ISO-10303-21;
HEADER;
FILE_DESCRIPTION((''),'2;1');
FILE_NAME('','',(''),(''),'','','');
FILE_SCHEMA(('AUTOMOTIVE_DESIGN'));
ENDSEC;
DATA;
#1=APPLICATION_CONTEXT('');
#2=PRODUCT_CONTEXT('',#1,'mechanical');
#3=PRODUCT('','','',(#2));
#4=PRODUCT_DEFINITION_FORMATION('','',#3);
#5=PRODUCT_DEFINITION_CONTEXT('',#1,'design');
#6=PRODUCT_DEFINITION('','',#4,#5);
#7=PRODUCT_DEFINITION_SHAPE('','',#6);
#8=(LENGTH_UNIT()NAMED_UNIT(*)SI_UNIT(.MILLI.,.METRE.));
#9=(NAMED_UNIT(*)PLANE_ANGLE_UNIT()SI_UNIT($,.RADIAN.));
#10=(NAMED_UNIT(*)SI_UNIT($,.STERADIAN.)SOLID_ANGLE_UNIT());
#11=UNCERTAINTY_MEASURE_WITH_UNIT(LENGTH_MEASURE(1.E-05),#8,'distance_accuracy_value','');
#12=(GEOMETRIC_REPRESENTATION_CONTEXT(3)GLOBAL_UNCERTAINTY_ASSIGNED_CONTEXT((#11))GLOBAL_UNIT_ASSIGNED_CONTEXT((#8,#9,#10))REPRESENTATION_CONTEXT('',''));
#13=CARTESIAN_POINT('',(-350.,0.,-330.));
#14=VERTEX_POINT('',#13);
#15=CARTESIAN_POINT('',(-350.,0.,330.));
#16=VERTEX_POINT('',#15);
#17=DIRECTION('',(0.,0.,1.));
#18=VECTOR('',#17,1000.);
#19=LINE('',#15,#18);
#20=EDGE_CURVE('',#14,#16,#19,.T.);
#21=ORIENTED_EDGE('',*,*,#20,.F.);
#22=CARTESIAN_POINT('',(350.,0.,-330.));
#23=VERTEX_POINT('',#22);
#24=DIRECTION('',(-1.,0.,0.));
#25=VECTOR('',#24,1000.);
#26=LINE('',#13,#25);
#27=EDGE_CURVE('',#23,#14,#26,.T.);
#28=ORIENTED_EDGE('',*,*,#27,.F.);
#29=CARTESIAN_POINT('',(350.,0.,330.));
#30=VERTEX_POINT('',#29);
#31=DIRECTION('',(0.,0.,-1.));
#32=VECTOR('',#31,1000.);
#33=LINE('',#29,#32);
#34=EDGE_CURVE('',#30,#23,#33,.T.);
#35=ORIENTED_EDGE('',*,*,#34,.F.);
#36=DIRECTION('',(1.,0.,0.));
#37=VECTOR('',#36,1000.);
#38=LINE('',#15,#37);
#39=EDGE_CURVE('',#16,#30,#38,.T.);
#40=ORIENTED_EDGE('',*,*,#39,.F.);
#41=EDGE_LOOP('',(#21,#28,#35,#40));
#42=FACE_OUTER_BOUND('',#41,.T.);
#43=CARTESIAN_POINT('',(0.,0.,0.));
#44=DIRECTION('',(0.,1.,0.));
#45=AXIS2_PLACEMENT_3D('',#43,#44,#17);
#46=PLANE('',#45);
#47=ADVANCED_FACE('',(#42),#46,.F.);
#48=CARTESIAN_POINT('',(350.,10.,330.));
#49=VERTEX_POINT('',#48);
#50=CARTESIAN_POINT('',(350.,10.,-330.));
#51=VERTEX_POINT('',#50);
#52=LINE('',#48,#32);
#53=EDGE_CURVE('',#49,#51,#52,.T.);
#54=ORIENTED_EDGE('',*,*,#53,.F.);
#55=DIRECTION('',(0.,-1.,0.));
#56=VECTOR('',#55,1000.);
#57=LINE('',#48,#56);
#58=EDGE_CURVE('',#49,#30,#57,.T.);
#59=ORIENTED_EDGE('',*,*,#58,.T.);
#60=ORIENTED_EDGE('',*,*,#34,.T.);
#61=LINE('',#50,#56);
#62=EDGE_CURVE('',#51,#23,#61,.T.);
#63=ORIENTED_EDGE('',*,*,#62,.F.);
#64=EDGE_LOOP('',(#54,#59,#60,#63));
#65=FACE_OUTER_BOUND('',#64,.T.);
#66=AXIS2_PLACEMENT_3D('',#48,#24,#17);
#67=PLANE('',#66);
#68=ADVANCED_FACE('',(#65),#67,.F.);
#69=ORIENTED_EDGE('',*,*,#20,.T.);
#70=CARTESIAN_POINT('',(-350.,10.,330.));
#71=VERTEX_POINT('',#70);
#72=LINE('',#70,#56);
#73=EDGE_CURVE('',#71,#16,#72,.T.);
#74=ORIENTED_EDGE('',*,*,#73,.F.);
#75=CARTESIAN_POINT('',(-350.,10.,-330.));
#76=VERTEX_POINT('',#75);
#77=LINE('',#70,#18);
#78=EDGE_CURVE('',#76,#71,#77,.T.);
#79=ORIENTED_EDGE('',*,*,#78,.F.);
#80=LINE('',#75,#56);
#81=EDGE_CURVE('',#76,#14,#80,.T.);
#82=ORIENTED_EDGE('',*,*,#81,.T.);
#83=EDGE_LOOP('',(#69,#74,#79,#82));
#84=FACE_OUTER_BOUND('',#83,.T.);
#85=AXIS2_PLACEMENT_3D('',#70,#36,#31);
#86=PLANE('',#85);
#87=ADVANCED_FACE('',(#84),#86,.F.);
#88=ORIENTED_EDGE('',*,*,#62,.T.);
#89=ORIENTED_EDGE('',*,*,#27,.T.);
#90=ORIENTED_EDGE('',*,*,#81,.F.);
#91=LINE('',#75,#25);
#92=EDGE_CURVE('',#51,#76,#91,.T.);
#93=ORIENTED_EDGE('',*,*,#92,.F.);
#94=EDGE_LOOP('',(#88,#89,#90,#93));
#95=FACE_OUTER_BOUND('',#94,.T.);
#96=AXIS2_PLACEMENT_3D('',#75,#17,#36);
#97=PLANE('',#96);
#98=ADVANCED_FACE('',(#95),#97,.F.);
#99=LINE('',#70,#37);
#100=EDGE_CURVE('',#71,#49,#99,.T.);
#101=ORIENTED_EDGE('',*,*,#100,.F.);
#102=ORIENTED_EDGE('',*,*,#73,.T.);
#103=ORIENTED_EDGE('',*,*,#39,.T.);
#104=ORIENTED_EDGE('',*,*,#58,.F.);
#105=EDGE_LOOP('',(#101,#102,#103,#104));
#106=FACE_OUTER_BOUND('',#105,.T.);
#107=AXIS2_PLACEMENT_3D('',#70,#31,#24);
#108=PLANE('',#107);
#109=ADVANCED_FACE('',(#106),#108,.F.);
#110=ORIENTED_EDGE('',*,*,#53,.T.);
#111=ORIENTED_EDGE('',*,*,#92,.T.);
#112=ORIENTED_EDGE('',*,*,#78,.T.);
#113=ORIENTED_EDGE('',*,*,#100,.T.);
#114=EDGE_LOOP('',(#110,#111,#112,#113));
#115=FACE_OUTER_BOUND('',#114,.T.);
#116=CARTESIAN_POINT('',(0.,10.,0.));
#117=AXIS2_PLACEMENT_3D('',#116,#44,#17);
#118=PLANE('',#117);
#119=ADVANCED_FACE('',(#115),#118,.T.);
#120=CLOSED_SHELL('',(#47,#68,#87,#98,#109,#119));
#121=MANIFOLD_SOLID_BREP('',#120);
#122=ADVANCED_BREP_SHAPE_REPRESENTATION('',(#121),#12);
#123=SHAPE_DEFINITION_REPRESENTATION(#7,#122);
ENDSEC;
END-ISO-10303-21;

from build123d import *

# Parameters (mm, degrees)
SKETCH1_W           = 700
SKETCH1_H           = 660
BOSS_EXTRUDE1_DEPTH = 10


with BuildPart() as part:
    # Sketch1 → Boss-Extrude1 (new body)
    with BuildSketch(Plane(origin=(0, 0, 0), x_dir=(1, 0, 0), z_dir=(0, 1, 0))):
        Rectangle(SKETCH1_W, SKETCH1_H)
    extrude(amount=BOSS_EXTRUDE1_DEPTH)


solid = part.part
